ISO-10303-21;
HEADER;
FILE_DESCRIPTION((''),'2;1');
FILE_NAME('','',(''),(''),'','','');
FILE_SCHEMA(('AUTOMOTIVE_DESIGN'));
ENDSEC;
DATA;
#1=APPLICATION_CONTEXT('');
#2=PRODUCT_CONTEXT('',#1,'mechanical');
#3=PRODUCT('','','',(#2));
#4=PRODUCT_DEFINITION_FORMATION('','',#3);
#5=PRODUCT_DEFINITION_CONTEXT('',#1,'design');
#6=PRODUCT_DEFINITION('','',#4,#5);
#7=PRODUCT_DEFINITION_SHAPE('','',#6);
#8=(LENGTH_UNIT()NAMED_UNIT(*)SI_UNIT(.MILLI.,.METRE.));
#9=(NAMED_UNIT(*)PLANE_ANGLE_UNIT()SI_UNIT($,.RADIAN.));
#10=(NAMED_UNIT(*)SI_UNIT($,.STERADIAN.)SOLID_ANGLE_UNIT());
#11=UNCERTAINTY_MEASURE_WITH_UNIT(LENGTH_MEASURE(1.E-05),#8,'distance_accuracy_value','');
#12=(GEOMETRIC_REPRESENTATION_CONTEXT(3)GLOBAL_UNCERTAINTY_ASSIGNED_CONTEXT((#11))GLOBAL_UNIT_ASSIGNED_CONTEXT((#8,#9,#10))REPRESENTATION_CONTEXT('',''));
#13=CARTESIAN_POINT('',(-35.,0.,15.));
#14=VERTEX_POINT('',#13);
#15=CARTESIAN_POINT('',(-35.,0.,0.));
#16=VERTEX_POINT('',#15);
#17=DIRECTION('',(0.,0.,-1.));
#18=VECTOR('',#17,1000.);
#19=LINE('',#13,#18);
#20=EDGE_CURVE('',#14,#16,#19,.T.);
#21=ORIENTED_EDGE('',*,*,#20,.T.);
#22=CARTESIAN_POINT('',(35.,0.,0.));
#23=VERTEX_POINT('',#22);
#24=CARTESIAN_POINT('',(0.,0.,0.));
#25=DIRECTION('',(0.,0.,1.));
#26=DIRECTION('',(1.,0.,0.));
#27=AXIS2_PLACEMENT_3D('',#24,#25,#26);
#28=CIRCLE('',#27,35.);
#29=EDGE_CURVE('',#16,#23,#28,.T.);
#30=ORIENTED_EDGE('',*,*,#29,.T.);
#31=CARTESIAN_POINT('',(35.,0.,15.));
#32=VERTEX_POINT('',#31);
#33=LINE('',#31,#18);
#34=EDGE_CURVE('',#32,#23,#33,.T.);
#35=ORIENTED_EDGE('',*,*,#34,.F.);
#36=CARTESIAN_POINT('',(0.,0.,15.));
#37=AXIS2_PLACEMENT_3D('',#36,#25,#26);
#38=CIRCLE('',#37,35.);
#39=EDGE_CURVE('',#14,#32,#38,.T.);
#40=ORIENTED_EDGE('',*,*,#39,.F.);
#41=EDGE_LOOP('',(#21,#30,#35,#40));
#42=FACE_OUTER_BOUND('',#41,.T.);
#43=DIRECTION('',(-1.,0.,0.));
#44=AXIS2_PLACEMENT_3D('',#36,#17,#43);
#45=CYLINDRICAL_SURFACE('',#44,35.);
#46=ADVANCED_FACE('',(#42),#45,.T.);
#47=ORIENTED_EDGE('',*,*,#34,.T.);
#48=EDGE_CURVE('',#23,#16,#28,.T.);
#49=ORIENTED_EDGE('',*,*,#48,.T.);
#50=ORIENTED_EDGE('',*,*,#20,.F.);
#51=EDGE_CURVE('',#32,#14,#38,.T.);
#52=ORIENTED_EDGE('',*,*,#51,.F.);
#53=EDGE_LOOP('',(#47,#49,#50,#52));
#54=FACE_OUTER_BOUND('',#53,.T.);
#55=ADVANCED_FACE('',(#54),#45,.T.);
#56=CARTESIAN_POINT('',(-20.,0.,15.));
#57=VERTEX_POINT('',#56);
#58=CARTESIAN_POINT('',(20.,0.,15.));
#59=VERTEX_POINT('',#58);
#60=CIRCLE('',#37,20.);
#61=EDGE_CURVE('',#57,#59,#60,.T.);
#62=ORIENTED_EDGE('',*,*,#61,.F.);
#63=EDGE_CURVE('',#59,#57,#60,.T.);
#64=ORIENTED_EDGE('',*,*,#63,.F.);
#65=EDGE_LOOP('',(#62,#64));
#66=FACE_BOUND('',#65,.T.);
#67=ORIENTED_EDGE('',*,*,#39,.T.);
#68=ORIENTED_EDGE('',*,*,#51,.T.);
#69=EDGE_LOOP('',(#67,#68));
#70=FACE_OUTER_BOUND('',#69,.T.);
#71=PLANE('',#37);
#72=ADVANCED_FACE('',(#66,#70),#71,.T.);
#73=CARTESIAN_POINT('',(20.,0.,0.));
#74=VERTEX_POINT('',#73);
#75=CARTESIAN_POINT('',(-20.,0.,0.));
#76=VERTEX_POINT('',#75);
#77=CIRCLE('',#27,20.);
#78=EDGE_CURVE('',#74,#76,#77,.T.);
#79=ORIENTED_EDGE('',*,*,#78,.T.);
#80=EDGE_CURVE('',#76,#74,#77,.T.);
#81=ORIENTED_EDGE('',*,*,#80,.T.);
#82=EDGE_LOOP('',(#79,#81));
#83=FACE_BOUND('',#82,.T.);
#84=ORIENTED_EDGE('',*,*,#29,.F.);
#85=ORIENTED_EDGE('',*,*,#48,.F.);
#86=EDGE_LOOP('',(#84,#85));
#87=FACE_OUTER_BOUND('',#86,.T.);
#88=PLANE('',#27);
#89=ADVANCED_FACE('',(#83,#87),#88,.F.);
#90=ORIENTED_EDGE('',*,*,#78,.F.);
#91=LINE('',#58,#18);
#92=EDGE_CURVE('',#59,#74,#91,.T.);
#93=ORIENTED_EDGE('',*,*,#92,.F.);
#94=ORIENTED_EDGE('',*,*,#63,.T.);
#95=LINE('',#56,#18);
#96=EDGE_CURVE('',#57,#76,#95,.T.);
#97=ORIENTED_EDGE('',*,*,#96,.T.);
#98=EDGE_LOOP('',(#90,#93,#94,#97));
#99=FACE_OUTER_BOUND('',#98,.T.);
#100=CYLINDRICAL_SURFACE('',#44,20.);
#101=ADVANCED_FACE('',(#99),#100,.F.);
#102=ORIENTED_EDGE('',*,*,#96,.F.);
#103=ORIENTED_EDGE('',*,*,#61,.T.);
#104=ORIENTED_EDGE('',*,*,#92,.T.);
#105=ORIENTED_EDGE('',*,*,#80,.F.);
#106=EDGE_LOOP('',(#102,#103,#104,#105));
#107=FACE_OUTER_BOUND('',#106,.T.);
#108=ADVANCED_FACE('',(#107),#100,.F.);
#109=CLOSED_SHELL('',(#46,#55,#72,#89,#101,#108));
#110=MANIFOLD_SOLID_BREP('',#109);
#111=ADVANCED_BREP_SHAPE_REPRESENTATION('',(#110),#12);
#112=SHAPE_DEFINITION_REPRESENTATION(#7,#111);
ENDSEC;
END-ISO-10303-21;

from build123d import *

# Parameters (mm, degrees)
SKETCH1_R           = 35
SKETCH1_R_2         = 20
BOSS_EXTRUDE1_DEPTH = 15


with BuildPart() as part:
    # Sketch1 → Boss-Extrude1 (new body)
    with BuildSketch(Plane.XY):
        Circle(SKETCH1_R)
        Circle(SKETCH1_R_2, mode=Mode.SUBTRACT)
    extrude(amount=BOSS_EXTRUDE1_DEPTH)


solid = part.part
